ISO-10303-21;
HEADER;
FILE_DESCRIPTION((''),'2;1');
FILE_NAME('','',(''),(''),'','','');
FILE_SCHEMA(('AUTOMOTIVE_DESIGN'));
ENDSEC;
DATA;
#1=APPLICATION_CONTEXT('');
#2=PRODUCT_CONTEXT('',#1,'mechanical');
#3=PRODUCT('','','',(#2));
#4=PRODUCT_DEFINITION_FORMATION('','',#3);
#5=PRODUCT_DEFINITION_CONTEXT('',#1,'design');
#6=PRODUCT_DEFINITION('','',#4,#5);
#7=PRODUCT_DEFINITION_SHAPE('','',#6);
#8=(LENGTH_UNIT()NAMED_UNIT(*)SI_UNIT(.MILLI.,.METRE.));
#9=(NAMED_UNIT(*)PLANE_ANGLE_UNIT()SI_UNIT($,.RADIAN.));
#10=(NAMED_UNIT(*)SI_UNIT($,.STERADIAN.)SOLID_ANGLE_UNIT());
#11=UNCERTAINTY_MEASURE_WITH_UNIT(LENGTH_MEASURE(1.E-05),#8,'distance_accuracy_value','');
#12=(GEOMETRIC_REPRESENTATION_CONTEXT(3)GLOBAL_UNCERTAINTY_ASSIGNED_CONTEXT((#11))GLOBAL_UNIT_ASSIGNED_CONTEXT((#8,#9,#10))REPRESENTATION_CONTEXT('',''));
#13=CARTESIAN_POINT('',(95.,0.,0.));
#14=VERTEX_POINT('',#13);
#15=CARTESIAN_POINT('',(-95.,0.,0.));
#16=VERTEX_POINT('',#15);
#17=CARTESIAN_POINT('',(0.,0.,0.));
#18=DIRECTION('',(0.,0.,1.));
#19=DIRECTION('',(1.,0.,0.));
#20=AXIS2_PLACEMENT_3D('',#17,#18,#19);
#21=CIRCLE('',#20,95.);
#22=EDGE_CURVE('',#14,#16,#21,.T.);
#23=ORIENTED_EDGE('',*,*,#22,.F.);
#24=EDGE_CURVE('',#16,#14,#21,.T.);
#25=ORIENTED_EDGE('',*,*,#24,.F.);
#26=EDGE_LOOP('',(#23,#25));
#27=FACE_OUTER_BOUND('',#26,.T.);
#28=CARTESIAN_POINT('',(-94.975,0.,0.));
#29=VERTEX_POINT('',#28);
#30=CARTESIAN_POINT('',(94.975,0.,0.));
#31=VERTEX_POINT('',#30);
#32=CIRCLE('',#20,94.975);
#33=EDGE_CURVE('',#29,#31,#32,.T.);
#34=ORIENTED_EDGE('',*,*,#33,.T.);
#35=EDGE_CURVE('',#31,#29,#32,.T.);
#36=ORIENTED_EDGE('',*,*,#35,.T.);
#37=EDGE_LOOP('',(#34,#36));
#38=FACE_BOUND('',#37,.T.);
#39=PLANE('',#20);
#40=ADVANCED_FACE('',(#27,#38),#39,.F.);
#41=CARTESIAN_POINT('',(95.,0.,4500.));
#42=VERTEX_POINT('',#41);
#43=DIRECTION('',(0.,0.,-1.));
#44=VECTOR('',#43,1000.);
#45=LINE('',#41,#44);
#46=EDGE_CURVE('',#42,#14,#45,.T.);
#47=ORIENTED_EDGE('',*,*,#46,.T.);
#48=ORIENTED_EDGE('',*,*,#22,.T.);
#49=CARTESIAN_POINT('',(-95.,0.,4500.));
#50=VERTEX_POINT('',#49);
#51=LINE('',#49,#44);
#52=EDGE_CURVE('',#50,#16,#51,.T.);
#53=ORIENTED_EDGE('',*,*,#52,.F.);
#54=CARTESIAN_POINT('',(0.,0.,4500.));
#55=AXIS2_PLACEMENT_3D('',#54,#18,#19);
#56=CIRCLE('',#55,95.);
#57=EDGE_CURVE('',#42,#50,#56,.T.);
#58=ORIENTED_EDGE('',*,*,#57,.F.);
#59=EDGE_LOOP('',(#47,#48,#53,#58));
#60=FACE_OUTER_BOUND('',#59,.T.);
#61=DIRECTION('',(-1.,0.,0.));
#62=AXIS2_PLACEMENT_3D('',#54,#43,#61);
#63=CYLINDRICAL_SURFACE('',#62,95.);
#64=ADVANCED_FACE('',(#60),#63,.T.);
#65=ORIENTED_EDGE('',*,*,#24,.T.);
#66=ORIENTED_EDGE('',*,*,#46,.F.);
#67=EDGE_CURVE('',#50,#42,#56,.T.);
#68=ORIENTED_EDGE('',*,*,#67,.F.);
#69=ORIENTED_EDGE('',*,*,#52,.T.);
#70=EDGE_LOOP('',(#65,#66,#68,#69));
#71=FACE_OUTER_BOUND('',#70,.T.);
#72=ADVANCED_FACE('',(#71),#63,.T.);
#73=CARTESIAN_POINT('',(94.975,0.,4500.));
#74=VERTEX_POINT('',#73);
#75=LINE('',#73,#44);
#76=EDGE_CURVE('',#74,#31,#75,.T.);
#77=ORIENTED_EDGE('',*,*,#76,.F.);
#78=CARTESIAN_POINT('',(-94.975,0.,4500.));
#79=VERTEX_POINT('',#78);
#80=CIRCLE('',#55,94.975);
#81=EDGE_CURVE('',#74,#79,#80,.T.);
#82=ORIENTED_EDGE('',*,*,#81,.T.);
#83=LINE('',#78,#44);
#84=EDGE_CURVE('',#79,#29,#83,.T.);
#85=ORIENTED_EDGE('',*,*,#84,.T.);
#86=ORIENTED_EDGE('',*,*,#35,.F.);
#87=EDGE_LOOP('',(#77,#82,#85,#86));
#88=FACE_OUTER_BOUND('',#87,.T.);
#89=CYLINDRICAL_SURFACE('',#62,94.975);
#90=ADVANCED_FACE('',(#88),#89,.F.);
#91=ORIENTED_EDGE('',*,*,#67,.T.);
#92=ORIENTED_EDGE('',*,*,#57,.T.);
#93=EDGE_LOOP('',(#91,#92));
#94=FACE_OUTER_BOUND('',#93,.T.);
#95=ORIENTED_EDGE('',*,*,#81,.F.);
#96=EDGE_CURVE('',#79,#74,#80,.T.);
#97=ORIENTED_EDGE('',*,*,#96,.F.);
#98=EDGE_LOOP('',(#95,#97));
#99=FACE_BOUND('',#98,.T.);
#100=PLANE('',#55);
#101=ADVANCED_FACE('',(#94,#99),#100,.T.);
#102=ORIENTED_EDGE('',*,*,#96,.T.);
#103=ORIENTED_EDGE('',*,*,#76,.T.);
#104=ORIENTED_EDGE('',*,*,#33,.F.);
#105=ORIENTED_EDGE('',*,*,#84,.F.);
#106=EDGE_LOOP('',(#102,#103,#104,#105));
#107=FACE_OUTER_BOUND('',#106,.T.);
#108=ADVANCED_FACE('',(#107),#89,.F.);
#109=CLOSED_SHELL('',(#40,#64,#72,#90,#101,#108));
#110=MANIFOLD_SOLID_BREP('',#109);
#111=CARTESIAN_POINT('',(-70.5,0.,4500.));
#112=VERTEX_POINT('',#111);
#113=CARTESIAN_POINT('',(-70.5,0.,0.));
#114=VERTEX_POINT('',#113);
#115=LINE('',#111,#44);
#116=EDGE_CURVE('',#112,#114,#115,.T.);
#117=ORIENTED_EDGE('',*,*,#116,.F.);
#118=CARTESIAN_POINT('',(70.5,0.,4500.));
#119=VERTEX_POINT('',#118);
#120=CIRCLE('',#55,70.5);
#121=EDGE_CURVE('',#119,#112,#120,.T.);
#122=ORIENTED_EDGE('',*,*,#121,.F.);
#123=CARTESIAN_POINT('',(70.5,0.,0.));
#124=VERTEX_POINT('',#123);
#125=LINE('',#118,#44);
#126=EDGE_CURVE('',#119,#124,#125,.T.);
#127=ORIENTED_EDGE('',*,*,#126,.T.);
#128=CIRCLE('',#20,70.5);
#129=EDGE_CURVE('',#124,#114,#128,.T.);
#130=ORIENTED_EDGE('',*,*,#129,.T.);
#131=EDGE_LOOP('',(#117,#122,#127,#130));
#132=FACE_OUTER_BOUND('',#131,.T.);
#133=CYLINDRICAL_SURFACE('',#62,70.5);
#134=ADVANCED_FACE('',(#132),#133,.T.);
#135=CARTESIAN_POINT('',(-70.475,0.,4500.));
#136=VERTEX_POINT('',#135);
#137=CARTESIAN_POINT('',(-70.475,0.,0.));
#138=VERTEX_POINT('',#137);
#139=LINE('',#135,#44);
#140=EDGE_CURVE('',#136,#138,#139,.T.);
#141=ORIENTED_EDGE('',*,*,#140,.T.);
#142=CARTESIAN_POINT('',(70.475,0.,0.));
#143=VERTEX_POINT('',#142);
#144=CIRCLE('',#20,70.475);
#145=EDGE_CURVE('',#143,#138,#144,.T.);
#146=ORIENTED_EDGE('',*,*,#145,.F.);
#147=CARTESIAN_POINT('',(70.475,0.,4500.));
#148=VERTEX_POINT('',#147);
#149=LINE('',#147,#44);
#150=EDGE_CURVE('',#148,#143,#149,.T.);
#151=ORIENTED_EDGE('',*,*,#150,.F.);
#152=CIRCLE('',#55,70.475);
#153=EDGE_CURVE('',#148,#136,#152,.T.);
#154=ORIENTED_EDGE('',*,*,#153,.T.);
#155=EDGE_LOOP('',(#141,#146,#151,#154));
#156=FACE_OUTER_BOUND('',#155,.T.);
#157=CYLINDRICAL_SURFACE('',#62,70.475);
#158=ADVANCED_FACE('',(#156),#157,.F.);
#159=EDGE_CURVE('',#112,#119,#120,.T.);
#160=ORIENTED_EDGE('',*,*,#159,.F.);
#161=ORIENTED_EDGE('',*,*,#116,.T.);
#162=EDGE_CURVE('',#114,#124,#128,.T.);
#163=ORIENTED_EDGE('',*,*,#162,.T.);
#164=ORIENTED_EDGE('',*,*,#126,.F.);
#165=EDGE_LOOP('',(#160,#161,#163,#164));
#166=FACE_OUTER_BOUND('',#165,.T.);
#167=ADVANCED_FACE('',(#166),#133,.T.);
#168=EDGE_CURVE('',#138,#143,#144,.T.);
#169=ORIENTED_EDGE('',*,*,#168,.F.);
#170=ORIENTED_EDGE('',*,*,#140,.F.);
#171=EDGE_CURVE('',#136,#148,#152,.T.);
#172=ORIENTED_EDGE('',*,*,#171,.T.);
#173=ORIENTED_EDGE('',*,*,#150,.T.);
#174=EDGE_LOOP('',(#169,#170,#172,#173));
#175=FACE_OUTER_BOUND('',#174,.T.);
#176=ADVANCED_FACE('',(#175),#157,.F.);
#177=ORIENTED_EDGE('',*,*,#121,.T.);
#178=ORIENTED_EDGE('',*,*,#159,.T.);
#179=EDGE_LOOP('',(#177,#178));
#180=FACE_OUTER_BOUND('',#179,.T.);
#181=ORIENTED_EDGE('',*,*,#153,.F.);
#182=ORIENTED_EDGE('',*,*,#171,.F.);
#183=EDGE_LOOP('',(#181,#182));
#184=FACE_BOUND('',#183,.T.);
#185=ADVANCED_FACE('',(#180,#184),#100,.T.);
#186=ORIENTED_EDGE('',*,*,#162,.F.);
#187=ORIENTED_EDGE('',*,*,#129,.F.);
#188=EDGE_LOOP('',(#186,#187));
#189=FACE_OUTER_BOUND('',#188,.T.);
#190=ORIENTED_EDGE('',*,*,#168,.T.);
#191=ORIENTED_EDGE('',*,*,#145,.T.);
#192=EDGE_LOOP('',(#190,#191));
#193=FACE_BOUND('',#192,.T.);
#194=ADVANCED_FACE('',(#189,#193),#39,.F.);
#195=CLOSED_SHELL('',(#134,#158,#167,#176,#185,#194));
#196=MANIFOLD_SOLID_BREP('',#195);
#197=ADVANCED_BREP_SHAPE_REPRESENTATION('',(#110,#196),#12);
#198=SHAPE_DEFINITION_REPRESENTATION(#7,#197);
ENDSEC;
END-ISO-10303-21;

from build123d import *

# Parameters (mm, degrees)
SKETCH1_R           = 95
SKETCH1_R_2         = 94.975
BOSS_EXTRUDE1_DEPTH = 4500
SKETCH2_R           = 70.5
SKETCH2_R_2         = 70.475
BOSS_EXTRUDE2_DEPTH = 4500


with BuildPart() as part:
    # Sketch1 → Boss-Extrude1 (new body)
    with BuildSketch(Plane.XY):
        Circle(SKETCH1_R)
        Circle(SKETCH1_R_2, mode=Mode.SUBTRACT)
    extrude(amount=BOSS_EXTRUDE1_DEPTH)


with BuildPart() as body_2:
    # Sketch2 → Boss-Extrude2 (new body)
    with BuildSketch(Plane.XY):
        Circle(SKETCH2_R)
        Circle(SKETCH2_R_2, mode=Mode.SUBTRACT)
    extrude(amount=BOSS_EXTRUDE2_DEPTH)


solid = Compound([part.part, body_2.part])
